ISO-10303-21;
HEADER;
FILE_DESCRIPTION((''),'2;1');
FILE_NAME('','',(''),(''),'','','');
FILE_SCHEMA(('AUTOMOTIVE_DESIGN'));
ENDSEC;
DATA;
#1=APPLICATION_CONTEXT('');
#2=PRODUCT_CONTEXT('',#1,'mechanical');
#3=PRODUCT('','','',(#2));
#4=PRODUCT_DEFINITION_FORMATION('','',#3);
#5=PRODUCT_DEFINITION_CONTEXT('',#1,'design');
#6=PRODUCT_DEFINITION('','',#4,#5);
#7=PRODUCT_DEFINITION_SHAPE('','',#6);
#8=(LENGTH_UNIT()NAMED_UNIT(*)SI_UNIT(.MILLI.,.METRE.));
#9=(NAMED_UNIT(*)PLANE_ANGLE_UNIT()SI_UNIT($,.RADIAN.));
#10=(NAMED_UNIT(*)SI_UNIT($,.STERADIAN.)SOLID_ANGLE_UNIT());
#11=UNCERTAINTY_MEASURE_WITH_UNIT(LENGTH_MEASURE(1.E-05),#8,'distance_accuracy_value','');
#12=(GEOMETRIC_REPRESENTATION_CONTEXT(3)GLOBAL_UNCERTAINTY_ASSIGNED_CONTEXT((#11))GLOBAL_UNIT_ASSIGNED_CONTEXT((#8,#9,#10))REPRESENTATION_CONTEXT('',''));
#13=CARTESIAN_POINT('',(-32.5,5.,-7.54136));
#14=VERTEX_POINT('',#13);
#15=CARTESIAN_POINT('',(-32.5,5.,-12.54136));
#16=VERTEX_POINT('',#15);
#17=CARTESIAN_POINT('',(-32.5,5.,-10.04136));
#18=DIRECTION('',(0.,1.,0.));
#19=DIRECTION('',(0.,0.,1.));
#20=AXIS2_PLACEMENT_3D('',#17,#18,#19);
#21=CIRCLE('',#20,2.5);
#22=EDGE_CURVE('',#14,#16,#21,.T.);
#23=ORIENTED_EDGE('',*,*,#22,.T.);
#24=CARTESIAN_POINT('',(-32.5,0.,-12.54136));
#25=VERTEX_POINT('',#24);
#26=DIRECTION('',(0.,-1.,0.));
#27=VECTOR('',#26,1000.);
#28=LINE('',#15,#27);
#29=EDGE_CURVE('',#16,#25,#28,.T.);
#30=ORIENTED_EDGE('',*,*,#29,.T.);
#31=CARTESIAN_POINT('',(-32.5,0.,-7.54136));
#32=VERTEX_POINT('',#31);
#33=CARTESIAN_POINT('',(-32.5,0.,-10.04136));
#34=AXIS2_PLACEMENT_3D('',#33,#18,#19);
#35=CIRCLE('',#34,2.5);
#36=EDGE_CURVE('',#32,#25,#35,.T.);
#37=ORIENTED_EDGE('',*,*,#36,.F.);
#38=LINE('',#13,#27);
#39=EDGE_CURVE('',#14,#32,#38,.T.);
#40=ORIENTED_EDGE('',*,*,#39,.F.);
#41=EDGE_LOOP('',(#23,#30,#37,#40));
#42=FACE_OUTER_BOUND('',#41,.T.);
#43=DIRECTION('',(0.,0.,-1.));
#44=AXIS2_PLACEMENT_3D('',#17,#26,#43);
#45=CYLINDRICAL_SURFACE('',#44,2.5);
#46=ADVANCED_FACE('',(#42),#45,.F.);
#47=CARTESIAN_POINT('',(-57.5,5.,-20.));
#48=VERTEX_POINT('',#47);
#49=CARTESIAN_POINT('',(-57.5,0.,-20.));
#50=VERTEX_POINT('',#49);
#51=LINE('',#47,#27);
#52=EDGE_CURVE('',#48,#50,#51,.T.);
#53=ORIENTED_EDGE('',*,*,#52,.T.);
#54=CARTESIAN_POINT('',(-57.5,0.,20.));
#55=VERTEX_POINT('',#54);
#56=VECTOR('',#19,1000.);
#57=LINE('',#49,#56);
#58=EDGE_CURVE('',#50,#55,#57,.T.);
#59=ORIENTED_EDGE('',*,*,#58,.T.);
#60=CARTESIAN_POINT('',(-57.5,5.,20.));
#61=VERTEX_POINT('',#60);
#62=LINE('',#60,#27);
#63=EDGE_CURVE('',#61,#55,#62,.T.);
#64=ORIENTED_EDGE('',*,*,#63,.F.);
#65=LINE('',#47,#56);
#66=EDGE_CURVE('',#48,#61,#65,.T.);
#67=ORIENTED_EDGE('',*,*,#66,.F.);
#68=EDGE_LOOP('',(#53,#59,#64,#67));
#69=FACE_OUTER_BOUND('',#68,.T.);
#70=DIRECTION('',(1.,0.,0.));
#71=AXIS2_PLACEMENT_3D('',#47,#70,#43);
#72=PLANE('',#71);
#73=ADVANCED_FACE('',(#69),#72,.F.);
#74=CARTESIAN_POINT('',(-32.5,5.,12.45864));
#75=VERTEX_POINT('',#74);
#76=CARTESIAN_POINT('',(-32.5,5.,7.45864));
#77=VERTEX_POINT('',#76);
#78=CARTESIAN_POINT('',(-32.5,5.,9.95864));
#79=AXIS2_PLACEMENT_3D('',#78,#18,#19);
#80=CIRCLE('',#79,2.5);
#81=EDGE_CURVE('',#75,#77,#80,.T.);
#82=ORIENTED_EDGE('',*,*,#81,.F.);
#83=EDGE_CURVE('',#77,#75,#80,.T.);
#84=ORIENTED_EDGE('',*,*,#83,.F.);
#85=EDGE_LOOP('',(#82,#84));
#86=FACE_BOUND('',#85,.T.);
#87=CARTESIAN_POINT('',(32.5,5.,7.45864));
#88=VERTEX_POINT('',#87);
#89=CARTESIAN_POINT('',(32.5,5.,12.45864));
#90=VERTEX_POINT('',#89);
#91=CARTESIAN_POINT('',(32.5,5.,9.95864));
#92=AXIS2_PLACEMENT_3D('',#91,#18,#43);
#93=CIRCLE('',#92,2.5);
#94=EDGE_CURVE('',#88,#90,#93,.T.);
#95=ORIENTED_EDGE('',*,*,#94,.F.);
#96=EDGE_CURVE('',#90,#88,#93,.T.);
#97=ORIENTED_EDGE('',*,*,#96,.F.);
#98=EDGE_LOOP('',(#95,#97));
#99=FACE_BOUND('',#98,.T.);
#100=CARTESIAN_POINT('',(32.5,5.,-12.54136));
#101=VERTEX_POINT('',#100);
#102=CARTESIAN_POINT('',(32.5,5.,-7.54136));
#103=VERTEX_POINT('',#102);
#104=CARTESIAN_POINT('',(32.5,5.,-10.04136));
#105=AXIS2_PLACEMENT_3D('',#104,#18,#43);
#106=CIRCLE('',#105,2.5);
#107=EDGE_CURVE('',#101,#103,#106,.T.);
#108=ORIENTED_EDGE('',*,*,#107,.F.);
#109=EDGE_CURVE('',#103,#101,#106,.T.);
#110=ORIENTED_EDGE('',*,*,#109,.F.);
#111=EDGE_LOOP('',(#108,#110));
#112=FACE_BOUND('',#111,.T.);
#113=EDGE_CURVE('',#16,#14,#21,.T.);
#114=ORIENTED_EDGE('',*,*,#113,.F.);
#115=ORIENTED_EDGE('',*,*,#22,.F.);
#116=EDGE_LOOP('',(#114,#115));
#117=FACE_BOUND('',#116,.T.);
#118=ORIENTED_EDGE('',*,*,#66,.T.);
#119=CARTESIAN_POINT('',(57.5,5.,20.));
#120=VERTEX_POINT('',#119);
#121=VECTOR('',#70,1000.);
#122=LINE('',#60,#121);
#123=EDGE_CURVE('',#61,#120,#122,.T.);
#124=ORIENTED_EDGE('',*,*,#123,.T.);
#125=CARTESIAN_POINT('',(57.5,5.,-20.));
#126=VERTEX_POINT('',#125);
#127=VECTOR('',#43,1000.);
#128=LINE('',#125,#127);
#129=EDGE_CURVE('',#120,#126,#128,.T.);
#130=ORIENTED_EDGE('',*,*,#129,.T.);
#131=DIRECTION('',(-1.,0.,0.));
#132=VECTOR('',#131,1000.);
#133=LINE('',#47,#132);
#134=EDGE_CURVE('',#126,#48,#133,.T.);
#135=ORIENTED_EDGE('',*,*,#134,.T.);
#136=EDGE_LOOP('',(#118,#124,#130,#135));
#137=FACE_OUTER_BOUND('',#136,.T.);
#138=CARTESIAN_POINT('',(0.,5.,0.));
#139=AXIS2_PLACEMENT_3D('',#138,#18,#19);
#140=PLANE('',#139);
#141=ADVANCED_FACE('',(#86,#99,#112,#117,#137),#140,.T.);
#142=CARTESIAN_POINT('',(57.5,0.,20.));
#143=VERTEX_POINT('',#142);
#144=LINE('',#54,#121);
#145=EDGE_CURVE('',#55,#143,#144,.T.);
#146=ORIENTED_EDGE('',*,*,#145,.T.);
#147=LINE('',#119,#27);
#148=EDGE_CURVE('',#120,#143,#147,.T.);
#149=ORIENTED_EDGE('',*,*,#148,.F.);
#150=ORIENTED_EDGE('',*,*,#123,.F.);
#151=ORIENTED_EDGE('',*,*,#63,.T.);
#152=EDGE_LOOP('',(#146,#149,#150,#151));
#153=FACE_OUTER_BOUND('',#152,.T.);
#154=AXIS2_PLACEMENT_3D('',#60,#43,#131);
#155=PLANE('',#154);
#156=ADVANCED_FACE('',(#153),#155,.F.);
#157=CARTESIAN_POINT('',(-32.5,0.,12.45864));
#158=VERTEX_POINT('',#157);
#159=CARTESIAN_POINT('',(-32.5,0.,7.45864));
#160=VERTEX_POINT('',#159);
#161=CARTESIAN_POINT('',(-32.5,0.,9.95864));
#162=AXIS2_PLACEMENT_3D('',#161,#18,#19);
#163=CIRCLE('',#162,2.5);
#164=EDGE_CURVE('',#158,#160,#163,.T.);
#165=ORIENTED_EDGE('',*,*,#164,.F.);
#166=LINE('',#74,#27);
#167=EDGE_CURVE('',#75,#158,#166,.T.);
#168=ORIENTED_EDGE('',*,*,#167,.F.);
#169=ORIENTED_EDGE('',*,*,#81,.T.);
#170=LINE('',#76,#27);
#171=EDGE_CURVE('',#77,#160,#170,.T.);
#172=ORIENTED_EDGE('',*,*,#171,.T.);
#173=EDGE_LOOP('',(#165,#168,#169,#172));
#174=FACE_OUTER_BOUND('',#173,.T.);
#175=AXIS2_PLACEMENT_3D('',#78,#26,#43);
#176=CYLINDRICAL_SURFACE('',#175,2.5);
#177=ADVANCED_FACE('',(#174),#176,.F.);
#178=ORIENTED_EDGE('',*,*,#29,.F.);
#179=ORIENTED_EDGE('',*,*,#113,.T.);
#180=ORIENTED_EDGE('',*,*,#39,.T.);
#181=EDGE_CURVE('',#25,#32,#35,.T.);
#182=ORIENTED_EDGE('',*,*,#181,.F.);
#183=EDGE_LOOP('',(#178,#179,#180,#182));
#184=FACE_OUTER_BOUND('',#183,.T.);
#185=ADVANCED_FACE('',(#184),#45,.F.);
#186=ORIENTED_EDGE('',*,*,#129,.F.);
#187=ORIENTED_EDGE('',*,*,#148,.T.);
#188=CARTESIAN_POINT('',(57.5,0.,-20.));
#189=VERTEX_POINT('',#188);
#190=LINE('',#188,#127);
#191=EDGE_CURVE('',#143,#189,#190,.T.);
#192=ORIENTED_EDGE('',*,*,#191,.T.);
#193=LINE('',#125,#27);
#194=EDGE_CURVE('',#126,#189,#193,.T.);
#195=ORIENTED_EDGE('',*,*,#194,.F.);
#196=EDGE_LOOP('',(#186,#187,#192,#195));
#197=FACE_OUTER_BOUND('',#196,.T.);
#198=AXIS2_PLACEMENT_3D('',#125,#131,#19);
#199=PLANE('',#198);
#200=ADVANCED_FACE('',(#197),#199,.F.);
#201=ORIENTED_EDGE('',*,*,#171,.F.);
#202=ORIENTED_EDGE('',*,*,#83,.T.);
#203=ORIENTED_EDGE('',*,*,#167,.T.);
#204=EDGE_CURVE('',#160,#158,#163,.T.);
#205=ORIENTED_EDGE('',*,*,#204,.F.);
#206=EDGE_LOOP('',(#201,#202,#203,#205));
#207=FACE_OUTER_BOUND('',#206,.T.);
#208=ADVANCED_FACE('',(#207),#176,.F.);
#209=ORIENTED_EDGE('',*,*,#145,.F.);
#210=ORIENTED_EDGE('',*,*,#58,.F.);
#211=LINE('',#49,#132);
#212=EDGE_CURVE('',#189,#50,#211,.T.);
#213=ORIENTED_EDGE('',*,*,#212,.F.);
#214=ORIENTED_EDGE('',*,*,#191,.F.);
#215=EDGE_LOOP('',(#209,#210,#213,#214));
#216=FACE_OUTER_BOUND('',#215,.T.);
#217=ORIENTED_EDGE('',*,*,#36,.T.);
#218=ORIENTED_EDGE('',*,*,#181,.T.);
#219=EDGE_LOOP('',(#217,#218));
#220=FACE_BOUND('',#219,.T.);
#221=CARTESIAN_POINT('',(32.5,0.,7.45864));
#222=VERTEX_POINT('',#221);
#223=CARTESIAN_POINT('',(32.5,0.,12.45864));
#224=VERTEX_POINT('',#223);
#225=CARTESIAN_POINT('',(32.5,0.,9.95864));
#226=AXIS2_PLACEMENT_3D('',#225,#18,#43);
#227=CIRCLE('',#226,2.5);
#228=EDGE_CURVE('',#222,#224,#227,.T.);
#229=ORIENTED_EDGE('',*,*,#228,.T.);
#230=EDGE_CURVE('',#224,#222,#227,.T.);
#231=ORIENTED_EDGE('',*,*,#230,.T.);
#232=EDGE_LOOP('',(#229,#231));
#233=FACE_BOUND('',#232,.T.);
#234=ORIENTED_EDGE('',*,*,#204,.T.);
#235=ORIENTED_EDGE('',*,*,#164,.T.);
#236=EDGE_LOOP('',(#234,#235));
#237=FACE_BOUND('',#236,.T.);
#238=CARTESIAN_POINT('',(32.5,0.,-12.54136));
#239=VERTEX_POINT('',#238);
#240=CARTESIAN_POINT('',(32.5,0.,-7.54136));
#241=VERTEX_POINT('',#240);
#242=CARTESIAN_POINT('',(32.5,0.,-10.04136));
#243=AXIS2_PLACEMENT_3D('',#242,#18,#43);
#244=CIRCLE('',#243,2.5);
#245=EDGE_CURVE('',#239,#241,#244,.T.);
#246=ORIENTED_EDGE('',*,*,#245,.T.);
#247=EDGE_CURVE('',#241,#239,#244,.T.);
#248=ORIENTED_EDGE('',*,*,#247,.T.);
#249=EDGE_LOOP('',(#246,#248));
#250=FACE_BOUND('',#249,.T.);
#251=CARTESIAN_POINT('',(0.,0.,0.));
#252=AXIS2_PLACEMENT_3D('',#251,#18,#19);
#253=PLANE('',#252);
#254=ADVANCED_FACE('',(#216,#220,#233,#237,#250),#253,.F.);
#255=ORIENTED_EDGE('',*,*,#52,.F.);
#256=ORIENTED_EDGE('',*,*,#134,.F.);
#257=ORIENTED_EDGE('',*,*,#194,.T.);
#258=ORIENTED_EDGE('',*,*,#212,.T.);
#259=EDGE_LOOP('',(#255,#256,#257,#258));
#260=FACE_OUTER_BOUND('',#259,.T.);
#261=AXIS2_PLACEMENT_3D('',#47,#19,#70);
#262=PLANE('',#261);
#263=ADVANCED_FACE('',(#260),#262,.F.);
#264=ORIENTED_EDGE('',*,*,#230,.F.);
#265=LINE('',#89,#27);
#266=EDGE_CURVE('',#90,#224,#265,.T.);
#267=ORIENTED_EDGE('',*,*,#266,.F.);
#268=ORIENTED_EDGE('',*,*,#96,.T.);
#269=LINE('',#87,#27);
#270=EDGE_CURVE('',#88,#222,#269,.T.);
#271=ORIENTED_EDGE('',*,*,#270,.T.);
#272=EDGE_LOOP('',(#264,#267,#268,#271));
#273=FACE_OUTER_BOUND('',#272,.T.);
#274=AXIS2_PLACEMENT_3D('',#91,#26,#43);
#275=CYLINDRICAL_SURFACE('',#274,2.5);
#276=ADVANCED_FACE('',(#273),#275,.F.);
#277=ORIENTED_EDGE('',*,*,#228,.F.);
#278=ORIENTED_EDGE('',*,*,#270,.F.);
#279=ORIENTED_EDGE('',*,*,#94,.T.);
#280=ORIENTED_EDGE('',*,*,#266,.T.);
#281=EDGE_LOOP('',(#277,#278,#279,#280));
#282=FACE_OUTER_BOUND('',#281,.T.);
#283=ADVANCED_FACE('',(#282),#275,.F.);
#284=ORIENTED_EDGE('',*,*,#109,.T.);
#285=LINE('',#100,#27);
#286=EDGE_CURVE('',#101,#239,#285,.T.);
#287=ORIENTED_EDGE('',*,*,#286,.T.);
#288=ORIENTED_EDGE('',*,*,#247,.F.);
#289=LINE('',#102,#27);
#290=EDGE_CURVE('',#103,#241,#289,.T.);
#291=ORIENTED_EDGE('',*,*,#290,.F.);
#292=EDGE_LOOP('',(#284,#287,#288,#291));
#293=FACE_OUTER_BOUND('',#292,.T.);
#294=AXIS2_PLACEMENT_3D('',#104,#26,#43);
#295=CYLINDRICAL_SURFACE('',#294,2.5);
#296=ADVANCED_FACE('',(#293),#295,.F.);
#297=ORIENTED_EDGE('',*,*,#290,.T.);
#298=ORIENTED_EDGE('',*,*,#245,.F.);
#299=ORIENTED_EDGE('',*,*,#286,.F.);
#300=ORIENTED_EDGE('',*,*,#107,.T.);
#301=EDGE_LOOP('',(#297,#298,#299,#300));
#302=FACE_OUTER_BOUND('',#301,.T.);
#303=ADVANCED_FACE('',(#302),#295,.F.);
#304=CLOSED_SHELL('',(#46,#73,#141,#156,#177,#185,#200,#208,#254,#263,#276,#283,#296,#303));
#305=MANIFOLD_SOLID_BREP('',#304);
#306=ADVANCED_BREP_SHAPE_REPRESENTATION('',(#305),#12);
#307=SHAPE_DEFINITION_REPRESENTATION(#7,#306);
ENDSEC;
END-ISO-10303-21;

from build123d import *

# Parameters (mm, degrees)
BASE_PLATE_PROFILE_WITH_4_HOLES_W = 115
BASE_PLATE_PROFILE_WITH_4_HOLES_H = 40
BASE_PLATE_PROFILE_WITH_4_HOLES_R = 2.5
BASE_PLATE_115X40X5_DEPTH         = 5


with BuildPart() as part:
    # Base Plate Profile with 4 Holes → Base Plate 115x40x5 (new body)
    with BuildSketch(Plane(origin=(0, 0, 0), x_dir=(1, 0, 0), z_dir=(0, 1, 0))):
        Rectangle(BASE_PLATE_PROFILE_WITH_4_HOLES_W, BASE_PLATE_PROFILE_WITH_4_HOLES_H)
        with Locations(Location((-32.5, 10.041360294, 0), (0, 0, 270))):
            Circle(BASE_PLATE_PROFILE_WITH_4_HOLES_R, mode=Mode.SUBTRACT)
        with Locations(Location((-32.5, -9.958639706, 0), (0, 0, 270))):
            Circle(BASE_PLATE_PROFILE_WITH_4_HOLES_R, mode=Mode.SUBTRACT)
        with Locations(Location((32.5, -9.958639706, 0), (0, 0, 90))):
            Circle(BASE_PLATE_PROFILE_WITH_4_HOLES_R, mode=Mode.SUBTRACT)
        with Locations(Location((32.5, 10.041360294, 0), (0, 0, 90))):
            Circle(BASE_PLATE_PROFILE_WITH_4_HOLES_R, mode=Mode.SUBTRACT)
    extrude(amount=BASE_PLATE_115X40X5_DEPTH)


solid = part.part
